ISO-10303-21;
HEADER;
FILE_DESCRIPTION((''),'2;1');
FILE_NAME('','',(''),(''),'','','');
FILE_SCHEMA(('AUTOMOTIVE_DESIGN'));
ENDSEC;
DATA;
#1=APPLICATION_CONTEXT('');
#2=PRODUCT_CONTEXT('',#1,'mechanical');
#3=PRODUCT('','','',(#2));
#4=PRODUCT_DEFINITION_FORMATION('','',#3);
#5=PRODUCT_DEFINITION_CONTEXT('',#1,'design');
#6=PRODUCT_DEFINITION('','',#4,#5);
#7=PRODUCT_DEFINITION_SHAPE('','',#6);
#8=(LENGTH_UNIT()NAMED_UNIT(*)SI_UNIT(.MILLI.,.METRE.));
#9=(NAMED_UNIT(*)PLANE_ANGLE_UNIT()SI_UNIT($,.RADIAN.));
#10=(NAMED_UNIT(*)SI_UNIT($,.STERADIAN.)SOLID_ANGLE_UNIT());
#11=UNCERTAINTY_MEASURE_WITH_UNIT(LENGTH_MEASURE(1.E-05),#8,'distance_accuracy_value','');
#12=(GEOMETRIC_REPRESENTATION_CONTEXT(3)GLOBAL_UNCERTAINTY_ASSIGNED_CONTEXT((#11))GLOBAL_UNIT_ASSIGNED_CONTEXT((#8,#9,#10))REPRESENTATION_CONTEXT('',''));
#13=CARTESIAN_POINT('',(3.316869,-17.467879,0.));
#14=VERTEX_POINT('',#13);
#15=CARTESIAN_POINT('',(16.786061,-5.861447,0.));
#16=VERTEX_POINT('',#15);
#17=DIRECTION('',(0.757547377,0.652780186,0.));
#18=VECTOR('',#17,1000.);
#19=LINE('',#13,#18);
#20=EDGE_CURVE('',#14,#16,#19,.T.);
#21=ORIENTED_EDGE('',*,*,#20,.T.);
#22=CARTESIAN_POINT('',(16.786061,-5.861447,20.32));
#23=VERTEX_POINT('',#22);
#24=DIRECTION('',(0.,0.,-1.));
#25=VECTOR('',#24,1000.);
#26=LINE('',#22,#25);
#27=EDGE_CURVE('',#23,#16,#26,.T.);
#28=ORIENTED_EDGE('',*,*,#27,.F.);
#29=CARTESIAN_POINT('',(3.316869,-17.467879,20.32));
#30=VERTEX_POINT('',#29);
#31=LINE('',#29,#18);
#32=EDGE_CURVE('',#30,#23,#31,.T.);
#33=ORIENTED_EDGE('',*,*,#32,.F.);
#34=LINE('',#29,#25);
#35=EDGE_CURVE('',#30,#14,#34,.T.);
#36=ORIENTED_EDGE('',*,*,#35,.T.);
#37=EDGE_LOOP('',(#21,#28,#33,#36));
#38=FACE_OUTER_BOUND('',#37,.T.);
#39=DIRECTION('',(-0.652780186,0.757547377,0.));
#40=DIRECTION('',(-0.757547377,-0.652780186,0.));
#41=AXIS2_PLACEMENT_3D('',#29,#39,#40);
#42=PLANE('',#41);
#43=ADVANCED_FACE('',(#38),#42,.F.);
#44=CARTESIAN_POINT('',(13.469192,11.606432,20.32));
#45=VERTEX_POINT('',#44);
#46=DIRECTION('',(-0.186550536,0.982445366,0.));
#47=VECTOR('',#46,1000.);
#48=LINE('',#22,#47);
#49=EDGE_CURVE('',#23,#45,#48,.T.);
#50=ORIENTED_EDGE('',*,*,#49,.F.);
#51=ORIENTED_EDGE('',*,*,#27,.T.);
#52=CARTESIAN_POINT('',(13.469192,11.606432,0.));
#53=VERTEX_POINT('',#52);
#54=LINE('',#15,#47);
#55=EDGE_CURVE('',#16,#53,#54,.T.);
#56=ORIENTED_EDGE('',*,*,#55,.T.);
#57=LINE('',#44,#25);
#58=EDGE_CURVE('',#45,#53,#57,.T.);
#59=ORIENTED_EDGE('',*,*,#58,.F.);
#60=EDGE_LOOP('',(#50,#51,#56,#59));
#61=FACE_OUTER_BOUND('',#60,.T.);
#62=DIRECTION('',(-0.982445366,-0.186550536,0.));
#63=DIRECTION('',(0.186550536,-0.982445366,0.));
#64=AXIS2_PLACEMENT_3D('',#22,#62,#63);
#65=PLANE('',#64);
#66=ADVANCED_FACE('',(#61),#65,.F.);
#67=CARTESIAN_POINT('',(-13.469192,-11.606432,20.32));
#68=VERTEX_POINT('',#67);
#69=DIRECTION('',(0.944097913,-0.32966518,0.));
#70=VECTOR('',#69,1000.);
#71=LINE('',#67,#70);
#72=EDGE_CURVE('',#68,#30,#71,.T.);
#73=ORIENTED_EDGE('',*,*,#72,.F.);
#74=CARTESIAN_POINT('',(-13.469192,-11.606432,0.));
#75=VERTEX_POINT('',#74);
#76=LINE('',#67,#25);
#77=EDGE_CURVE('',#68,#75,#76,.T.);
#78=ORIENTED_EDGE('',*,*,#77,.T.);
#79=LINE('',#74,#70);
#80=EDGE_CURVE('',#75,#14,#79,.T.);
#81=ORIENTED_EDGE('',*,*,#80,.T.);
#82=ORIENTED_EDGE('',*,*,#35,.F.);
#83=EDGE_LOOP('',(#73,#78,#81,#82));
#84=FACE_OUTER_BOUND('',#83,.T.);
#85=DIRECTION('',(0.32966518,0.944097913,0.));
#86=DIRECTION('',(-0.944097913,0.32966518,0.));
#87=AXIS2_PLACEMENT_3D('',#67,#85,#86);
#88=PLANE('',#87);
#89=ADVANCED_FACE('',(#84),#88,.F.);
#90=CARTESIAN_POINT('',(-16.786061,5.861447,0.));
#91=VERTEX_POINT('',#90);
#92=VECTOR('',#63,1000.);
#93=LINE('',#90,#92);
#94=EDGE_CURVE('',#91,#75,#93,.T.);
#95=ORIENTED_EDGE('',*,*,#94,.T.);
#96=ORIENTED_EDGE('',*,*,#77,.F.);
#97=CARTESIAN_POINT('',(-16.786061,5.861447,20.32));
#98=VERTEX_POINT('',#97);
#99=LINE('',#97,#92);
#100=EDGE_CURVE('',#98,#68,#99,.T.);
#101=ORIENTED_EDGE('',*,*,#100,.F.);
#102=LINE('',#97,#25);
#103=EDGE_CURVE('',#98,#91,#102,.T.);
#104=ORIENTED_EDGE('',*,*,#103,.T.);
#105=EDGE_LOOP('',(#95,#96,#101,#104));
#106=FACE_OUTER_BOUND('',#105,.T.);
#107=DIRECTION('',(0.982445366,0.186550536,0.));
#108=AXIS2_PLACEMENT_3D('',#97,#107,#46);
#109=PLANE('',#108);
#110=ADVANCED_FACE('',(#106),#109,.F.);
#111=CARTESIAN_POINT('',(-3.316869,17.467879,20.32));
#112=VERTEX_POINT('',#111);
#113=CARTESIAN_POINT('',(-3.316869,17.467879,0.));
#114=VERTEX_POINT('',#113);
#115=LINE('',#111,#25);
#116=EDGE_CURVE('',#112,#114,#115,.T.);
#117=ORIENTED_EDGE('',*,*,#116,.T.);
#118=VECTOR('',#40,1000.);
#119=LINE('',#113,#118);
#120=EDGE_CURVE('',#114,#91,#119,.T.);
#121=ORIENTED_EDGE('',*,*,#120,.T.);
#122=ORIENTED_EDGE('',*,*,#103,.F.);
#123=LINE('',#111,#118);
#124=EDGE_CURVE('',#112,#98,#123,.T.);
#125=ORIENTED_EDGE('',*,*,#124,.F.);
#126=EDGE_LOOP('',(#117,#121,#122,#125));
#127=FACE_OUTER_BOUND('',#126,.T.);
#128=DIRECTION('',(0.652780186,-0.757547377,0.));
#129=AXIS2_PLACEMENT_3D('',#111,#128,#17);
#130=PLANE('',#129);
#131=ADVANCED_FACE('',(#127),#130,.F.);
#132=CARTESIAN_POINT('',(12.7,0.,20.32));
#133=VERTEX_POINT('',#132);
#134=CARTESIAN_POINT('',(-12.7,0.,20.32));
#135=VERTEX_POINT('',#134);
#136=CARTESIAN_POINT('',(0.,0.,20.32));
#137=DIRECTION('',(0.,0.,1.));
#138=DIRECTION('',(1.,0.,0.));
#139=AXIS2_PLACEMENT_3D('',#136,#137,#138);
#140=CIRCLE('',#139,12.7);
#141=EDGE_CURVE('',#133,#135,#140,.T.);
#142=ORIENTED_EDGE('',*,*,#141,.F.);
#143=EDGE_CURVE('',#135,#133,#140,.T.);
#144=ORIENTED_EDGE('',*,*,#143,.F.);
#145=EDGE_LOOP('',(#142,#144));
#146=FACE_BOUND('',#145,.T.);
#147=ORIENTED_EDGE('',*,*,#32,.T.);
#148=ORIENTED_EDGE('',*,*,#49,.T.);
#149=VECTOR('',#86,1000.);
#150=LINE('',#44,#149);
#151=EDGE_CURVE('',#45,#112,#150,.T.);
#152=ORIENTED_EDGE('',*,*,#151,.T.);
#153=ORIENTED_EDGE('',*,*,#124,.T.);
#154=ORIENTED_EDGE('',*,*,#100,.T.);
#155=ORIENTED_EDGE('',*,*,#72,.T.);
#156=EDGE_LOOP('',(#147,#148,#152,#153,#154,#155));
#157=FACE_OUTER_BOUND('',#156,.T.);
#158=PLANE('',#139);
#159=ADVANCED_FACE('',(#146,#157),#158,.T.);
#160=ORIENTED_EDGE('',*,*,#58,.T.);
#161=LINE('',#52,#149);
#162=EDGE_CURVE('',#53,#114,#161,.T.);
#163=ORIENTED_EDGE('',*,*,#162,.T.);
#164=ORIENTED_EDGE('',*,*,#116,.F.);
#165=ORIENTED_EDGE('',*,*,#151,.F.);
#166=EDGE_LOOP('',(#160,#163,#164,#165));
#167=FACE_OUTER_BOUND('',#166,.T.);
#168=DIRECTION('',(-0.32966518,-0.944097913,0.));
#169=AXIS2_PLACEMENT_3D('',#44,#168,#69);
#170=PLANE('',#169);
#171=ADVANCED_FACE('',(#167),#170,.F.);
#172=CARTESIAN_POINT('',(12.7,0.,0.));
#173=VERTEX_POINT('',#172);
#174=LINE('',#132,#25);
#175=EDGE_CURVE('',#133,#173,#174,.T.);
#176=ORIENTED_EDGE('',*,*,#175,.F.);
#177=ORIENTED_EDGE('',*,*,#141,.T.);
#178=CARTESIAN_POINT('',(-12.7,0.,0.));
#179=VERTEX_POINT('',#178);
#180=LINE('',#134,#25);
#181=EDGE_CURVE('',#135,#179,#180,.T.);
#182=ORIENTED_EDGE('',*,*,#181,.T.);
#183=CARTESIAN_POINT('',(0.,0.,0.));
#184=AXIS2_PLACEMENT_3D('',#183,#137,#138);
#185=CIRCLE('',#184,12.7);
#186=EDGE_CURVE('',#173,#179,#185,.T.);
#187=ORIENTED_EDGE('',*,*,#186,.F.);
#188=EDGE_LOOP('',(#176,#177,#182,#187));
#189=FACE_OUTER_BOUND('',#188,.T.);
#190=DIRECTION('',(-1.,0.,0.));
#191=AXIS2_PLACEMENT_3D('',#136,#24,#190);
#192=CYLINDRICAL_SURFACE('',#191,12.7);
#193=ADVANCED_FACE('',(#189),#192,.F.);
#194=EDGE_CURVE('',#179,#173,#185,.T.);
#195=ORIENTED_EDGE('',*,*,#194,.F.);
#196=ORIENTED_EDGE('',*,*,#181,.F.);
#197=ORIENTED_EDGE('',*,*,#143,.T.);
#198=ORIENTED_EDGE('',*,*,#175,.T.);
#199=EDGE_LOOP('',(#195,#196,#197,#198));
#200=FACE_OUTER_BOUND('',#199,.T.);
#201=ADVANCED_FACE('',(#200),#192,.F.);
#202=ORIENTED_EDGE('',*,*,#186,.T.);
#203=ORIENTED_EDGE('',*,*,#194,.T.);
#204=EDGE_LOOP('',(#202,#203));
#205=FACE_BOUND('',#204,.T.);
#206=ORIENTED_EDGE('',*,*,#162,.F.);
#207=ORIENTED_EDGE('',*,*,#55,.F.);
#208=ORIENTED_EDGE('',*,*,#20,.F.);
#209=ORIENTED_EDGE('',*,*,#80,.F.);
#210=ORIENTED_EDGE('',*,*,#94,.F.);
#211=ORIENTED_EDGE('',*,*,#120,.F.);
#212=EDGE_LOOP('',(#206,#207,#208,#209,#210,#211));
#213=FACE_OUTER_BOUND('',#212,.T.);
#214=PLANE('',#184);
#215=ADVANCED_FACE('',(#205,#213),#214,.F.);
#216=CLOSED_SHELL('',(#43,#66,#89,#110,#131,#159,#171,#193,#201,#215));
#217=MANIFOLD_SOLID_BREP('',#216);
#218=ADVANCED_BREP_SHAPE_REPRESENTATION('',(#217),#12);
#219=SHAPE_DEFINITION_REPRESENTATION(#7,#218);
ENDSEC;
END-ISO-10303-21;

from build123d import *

# Parameters (mm, degrees)
SKETCH1_R           = 6.35
BOSS_EXTRUDE1_DEPTH = 10.16
SCALE1_SCALE        = 2


with BuildPart() as part:
    # Sketch1 → Boss-Extrude1 (new body)
    with BuildSketch(Plane.XY):
        Polygon((6.73459618, 5.803215857), (-1.658434266, 8.733939305), (-8.393030446, 2.930723448), (-6.73459618, -5.803215857), (1.658434266, -8.733939305), (8.393030446, -2.930723448), align=None)
        Circle(SKETCH1_R, mode=Mode.SUBTRACT)
    extrude(amount=BOSS_EXTRUDE1_DEPTH)


with BuildPart() as part_1:
    # Scale1: scaled about (0, 0, 0)
    add(part.part.scale(SCALE1_SCALE))


solid = part_1.part
